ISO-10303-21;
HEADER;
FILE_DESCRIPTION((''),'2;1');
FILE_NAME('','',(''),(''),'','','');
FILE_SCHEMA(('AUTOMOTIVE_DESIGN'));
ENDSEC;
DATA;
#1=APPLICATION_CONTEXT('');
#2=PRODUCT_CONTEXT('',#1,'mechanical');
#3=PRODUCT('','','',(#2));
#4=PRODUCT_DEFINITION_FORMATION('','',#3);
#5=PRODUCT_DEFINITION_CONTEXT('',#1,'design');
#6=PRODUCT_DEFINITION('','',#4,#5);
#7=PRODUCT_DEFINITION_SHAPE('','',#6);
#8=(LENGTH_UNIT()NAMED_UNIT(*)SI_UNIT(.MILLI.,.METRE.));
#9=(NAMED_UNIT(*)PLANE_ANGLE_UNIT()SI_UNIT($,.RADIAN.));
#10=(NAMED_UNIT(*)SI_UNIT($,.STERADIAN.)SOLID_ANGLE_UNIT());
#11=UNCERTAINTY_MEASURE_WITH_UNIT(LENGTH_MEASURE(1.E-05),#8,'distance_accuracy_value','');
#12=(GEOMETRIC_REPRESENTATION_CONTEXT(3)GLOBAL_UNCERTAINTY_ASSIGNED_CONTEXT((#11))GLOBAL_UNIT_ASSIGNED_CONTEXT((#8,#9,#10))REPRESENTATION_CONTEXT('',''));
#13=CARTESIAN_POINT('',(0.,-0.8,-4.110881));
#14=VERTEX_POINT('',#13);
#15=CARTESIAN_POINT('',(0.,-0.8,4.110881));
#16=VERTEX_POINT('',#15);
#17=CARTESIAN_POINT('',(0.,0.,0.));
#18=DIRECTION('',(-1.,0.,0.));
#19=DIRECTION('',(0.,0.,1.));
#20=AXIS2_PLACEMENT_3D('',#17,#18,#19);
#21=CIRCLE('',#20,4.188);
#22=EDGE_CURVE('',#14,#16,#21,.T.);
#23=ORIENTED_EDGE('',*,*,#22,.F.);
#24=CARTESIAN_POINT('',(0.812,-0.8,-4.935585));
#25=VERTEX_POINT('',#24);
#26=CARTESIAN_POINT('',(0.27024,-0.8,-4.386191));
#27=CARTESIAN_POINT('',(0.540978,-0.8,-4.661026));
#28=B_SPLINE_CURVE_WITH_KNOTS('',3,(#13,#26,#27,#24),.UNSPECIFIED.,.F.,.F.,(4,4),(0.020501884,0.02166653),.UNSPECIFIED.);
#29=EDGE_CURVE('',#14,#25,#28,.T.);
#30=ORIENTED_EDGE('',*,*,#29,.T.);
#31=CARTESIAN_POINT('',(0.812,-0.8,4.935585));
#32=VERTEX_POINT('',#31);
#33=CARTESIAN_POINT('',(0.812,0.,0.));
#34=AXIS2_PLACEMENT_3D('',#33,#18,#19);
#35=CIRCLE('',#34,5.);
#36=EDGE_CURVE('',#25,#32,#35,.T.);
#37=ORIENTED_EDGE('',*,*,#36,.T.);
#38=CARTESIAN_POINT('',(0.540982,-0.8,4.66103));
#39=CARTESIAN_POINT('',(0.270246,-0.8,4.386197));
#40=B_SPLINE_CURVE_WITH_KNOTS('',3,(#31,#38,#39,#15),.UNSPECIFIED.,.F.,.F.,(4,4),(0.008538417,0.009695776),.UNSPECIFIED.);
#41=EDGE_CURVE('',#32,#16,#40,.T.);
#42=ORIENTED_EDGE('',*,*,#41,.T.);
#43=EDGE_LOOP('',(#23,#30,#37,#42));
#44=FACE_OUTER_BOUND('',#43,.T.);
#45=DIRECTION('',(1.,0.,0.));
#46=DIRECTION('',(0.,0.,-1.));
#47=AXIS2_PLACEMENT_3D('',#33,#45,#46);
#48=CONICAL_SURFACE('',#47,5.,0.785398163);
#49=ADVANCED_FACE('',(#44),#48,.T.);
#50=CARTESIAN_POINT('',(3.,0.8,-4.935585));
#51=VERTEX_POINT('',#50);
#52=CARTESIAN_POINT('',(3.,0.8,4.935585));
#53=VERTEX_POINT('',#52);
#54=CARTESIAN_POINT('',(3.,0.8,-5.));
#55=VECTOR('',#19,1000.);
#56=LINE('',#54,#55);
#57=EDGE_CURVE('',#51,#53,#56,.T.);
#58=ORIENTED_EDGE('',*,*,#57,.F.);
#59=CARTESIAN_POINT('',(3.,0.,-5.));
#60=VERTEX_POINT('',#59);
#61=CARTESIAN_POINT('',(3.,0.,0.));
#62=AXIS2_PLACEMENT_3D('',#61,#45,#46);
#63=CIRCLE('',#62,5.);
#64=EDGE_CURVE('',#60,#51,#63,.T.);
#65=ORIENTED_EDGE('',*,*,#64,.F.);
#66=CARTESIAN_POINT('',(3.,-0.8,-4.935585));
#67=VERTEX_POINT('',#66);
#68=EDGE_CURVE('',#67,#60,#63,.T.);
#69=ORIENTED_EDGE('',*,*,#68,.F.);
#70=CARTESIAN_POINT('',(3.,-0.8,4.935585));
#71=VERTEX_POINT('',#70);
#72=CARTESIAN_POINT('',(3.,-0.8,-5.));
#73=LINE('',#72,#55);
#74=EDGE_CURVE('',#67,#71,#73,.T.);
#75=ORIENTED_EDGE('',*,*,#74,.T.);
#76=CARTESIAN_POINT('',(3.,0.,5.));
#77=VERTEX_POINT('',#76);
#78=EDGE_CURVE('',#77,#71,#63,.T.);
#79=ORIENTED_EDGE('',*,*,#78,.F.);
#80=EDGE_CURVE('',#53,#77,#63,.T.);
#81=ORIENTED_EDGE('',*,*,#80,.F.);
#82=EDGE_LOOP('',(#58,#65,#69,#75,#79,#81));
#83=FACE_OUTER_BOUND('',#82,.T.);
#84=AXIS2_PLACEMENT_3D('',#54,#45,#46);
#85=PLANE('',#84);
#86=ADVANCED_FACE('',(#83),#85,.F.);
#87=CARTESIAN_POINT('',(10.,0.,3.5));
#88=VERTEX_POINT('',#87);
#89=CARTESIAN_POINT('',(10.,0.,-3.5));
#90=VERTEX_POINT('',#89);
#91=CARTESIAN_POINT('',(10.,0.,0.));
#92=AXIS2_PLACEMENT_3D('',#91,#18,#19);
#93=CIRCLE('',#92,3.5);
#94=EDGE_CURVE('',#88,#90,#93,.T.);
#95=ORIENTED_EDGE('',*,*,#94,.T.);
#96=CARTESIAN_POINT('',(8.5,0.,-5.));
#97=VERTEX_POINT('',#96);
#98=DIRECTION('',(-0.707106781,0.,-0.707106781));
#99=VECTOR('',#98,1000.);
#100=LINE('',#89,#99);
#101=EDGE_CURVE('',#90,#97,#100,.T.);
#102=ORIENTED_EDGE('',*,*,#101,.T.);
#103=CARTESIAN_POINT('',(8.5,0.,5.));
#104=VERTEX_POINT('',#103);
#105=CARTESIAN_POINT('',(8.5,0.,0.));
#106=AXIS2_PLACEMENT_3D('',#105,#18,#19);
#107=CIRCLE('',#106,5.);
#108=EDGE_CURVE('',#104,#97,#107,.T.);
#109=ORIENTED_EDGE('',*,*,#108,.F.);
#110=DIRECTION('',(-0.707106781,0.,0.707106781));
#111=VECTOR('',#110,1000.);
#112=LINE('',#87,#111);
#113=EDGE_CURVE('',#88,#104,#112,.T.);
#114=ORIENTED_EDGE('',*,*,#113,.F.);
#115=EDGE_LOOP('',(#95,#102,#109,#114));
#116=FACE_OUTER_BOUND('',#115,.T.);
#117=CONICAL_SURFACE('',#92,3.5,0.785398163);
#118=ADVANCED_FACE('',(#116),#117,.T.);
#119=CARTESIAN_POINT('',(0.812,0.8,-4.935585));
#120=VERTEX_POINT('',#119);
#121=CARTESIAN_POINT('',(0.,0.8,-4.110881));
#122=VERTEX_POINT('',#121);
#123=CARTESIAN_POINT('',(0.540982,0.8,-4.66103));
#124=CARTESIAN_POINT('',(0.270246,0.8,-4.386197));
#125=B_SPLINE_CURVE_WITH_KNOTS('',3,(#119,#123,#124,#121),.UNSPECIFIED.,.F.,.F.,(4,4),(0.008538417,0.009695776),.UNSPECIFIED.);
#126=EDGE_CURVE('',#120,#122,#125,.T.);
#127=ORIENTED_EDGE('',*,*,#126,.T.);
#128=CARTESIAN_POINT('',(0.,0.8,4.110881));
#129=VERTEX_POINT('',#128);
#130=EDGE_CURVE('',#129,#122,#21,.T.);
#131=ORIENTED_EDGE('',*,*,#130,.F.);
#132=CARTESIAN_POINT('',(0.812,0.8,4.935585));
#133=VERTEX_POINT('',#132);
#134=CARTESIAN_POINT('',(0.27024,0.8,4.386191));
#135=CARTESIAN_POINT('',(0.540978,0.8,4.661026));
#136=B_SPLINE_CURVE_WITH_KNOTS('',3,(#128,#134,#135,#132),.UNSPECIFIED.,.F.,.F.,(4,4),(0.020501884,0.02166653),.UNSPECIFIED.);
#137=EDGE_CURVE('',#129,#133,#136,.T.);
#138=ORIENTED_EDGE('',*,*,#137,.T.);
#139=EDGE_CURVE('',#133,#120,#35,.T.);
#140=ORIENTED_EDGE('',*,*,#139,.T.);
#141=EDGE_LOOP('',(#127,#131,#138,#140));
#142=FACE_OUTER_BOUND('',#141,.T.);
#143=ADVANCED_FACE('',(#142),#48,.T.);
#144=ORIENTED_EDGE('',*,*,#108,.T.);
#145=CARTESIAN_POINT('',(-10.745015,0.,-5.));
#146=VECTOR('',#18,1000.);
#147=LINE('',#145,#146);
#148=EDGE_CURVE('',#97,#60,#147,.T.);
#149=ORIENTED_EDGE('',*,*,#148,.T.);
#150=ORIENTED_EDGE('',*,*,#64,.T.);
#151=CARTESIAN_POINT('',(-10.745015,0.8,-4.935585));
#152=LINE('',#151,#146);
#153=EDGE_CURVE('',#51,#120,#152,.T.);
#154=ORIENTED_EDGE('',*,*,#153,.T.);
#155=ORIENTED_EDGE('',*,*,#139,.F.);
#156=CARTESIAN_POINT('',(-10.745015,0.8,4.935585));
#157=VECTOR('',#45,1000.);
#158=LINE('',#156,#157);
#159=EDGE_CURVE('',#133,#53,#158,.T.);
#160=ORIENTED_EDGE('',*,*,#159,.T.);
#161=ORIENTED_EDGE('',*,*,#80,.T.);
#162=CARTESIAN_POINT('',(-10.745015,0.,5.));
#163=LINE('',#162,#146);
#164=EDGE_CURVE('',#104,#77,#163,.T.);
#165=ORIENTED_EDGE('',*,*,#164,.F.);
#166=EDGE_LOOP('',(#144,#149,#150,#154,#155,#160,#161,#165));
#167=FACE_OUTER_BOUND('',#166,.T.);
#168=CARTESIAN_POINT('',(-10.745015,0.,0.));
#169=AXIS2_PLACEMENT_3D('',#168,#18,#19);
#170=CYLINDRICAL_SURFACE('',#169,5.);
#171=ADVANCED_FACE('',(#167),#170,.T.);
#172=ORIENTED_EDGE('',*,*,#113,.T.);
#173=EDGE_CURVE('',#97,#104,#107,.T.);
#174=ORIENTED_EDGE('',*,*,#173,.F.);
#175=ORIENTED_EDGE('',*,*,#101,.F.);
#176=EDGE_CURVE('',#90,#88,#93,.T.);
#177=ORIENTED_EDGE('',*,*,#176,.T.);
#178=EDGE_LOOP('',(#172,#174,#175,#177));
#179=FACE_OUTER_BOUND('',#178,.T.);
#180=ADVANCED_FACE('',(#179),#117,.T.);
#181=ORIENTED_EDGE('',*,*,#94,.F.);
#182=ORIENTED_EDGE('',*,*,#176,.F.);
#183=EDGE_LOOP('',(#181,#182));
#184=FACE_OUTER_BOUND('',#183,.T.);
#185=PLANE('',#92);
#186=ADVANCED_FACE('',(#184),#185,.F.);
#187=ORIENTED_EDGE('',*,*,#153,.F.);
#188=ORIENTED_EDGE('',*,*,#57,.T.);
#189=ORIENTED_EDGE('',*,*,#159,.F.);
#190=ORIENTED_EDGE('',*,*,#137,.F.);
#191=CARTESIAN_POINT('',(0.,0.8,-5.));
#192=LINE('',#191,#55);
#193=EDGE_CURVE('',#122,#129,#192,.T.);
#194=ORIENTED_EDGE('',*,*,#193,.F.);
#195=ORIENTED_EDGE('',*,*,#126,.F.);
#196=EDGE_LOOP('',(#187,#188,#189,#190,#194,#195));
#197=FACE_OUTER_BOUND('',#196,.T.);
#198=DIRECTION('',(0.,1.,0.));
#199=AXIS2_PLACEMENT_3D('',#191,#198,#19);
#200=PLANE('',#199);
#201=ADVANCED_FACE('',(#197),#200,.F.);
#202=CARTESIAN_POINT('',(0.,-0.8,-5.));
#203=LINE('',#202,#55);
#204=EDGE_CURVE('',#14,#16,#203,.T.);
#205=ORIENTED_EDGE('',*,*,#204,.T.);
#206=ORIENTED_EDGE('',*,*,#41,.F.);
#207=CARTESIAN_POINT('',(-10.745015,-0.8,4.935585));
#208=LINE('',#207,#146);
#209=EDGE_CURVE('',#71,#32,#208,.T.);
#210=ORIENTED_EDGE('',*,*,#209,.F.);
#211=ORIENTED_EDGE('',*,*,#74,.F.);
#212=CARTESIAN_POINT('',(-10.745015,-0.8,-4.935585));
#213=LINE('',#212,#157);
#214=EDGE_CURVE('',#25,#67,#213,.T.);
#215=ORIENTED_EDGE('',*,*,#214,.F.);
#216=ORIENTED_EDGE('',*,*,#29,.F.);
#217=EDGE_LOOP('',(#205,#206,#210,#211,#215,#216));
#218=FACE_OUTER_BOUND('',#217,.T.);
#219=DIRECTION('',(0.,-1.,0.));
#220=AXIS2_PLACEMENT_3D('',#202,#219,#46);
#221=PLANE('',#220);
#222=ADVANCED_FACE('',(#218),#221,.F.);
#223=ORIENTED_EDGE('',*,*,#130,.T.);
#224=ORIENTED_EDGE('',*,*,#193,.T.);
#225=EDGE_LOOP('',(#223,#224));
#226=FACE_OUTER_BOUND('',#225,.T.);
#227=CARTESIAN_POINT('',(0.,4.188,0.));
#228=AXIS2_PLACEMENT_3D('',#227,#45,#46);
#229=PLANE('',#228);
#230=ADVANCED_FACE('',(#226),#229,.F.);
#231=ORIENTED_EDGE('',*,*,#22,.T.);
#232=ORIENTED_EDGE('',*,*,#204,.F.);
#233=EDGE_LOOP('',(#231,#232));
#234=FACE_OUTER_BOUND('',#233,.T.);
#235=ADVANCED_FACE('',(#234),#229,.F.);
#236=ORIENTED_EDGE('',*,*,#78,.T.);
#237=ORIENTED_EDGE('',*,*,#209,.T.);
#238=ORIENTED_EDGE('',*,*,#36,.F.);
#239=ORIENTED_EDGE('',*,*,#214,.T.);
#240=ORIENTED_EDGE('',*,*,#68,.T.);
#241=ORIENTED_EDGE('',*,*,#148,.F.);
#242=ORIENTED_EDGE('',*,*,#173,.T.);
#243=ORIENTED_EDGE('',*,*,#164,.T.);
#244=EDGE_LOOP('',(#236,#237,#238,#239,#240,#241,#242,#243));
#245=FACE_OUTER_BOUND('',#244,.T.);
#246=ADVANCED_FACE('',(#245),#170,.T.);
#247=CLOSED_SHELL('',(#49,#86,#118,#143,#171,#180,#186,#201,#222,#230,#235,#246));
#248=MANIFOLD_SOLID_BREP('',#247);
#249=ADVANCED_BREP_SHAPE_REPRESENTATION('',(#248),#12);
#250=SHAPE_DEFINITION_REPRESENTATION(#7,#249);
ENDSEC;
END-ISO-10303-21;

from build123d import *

# Parameters (mm, degrees)
NOTCH_DEPTH      = 13.247448714
NOTCH_DEPTH_BACK = 13.247448714
SKETCH2_W        = 3
SKETCH2_H        = 1.6


with BuildPart() as part:
    # Sketch1 → Base (revolve)
    with BuildSketch(Plane.XY, mode=Mode.PRIVATE) as base_sk:
        Polygon((0, 0), (10, 0), (10, 3.5), (8.5, 5), (0.812, 5), (0, 4.188), align=None)
    revolve(base_sk.sketch.rotate(Axis((-10.745014543, 0, 0), (1, 0, 0)), 90), axis=Axis((-10.745014543, 0, 0), (1, 0, 0)))

    # Sketch2 → Notch (cut, two sides: drawn at the far end of the back side and taken through both)
    with BuildSketch(Plane.XY.offset(-NOTCH_DEPTH_BACK)):
        with Locations((1.5, 0)):
            Rectangle(SKETCH2_W, SKETCH2_H)
    extrude(amount=NOTCH_DEPTH + NOTCH_DEPTH_BACK, mode=Mode.SUBTRACT)


solid = part.part
